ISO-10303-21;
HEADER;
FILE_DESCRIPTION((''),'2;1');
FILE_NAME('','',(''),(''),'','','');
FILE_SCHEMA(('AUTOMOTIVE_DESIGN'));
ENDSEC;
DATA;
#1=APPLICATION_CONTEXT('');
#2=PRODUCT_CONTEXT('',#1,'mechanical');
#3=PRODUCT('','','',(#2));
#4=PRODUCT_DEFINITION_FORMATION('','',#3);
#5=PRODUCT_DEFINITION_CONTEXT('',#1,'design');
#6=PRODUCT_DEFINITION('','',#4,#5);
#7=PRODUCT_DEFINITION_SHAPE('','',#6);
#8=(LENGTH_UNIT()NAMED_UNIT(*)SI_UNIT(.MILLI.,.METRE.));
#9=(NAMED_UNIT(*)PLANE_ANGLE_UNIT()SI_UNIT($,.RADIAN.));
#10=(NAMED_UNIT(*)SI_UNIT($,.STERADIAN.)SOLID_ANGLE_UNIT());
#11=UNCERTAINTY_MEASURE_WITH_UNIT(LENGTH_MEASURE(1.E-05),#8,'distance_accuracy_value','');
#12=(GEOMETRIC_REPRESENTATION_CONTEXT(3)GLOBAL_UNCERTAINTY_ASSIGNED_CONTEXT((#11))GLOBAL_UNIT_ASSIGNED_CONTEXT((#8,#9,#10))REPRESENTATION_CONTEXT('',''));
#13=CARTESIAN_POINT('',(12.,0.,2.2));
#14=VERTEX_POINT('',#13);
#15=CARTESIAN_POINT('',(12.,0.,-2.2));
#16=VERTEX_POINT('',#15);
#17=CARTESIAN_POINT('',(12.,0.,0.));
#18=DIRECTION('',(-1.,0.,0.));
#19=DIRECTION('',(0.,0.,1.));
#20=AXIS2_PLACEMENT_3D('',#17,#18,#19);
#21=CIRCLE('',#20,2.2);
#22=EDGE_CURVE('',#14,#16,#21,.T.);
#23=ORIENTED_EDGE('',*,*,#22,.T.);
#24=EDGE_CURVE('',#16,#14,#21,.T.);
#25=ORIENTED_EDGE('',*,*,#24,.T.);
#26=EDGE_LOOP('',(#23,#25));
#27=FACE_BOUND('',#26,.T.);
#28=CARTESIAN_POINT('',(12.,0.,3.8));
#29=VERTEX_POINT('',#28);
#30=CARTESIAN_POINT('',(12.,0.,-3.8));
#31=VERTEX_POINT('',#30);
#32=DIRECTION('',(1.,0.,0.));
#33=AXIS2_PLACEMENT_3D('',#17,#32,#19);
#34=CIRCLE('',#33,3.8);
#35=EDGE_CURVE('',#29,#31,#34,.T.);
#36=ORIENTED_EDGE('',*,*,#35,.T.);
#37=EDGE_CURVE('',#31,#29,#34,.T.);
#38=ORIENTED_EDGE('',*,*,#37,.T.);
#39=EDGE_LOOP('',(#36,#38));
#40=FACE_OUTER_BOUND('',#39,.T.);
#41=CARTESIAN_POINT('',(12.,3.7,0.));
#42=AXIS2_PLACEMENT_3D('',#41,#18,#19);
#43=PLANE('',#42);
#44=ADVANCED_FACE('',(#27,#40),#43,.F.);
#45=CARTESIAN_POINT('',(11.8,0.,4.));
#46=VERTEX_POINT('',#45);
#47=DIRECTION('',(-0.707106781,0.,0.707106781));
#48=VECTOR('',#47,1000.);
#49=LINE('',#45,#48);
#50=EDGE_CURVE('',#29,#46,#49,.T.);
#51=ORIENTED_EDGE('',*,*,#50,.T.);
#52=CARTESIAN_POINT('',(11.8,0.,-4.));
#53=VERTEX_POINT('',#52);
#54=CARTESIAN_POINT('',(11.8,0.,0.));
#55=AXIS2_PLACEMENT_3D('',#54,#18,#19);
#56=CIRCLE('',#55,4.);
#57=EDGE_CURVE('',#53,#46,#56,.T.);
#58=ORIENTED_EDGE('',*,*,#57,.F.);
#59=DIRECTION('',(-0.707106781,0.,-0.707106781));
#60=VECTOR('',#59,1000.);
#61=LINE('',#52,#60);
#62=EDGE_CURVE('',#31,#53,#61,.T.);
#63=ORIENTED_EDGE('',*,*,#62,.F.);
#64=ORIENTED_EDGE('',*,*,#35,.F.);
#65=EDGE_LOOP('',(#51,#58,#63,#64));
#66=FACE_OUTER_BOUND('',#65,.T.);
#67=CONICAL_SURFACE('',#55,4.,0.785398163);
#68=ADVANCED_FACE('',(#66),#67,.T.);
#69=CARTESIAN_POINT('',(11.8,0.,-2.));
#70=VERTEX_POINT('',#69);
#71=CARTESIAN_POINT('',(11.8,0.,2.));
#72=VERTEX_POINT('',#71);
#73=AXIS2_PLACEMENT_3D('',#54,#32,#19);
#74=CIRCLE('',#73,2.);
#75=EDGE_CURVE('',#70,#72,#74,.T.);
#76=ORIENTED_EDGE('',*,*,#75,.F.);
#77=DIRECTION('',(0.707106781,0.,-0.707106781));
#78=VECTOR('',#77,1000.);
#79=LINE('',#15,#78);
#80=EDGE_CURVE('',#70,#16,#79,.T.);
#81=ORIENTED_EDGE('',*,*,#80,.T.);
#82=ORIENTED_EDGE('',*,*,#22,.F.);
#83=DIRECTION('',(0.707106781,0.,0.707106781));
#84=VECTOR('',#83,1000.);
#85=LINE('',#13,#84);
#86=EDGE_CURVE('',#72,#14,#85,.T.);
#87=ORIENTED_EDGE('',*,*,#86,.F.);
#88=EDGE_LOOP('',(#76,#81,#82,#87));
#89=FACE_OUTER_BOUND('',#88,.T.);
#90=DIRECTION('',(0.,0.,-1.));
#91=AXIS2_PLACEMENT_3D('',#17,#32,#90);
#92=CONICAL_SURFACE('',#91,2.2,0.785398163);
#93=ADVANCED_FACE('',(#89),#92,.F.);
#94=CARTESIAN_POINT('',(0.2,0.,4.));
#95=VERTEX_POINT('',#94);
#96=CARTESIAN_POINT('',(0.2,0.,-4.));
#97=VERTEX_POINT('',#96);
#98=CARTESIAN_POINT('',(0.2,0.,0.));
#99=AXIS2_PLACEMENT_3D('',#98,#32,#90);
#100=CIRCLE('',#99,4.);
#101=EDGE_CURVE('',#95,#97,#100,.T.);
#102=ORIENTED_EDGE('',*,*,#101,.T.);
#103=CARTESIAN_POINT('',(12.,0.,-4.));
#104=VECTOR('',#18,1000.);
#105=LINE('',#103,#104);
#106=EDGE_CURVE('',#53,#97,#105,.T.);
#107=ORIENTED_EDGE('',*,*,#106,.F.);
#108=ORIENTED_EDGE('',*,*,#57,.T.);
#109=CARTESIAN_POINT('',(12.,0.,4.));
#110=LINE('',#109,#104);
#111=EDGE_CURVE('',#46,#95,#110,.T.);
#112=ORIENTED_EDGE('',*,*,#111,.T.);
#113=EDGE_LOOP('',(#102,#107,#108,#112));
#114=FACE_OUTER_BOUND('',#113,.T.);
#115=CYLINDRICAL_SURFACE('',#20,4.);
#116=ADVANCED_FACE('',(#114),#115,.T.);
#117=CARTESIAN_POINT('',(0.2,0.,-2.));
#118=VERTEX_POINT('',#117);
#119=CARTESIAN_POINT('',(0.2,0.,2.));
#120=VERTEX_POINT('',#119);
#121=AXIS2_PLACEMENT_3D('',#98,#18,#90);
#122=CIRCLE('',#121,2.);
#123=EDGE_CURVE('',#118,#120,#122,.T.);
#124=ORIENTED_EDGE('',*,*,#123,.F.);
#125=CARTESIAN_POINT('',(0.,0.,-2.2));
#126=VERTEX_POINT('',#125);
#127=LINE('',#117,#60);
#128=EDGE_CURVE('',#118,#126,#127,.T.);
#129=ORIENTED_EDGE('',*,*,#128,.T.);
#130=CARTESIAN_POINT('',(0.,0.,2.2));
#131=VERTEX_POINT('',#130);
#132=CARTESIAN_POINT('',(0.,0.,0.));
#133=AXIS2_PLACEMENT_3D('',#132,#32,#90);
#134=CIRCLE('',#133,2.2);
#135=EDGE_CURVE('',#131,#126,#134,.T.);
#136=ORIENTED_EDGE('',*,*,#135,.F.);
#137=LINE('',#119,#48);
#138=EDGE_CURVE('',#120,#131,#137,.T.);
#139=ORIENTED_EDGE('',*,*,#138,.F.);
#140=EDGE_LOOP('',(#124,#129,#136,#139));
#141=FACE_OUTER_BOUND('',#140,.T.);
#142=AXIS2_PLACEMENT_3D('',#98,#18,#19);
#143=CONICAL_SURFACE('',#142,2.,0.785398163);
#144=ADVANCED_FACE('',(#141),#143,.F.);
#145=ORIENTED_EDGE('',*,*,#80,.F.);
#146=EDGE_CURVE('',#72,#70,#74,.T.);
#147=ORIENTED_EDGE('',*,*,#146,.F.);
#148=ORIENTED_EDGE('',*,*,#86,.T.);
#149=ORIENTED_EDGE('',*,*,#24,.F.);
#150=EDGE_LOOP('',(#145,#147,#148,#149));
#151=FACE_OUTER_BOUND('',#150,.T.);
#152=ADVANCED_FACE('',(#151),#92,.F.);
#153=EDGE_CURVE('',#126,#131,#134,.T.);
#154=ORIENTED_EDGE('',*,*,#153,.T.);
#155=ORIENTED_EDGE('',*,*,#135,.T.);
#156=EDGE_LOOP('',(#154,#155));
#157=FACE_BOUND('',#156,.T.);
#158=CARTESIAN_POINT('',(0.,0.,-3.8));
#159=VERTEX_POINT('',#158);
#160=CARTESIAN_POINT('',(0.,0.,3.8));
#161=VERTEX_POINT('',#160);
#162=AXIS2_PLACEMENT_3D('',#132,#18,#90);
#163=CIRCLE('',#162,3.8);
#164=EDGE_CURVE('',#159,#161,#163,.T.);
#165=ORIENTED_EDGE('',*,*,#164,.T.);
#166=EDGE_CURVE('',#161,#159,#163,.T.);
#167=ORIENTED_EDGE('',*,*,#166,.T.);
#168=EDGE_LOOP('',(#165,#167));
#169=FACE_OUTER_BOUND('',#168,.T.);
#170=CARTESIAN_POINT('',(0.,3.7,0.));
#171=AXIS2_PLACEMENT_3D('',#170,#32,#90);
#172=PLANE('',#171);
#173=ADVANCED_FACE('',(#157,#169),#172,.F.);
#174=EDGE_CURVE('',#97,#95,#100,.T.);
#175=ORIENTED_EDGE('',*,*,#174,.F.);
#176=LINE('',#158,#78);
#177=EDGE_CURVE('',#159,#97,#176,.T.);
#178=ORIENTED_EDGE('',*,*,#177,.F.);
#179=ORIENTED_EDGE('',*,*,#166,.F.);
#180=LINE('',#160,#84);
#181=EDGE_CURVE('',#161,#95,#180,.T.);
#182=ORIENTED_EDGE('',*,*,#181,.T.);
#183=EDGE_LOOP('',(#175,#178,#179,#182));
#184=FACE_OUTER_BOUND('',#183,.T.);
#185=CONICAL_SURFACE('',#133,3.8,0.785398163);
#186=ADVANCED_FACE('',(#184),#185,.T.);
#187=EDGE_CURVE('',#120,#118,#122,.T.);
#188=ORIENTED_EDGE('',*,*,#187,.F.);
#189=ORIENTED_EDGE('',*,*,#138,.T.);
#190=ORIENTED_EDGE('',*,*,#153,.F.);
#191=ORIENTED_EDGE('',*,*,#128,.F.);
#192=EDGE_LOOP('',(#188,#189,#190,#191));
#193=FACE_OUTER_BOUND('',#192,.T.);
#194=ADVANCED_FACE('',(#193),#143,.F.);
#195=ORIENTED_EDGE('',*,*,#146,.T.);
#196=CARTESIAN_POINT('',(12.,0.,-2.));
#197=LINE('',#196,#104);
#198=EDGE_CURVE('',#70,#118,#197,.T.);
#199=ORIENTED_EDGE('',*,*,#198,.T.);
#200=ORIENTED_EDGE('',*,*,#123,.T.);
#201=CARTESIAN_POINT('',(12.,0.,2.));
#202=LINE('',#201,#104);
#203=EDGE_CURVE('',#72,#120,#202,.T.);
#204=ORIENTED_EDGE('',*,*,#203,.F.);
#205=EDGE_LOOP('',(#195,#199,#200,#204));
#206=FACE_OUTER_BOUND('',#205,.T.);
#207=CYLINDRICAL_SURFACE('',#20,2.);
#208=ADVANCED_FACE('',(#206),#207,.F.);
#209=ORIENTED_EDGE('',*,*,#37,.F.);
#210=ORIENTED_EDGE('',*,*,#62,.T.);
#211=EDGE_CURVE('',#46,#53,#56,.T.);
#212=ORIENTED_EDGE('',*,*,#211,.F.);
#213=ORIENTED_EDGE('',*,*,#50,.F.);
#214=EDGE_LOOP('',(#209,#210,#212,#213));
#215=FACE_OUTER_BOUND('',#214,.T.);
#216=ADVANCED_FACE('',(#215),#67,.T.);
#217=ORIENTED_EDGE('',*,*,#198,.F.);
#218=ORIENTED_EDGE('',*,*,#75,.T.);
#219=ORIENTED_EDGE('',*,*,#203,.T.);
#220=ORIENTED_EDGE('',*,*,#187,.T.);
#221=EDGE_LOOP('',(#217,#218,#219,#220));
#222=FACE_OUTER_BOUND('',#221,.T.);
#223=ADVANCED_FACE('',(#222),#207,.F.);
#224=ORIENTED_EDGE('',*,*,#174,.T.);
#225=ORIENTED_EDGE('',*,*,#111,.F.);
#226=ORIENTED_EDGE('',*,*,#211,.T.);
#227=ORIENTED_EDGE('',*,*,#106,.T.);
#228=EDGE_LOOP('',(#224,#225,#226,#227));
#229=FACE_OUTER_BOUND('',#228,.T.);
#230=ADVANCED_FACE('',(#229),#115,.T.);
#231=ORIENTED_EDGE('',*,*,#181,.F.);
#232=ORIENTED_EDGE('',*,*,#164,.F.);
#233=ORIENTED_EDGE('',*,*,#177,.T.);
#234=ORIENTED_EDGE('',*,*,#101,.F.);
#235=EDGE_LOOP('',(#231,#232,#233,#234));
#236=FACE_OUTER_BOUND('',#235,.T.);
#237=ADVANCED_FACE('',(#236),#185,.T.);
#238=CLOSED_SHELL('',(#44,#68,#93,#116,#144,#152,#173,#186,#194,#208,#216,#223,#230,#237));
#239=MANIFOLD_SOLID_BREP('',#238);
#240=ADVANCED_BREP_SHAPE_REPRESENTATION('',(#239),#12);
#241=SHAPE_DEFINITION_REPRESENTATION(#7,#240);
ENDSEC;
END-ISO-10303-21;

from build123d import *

# Parameters (mm, degrees)
CHAMFER1_SIZE = 0.2


with BuildPart() as part:
    # Sketch1 → Revolve1 (revolve)
    with BuildSketch(Plane.XY, mode=Mode.PRIVATE) as revolve1_sk:
        Polygon((0, 3.7), (0, 2), (12, 2), (12, 3.7), (12, 4), (11.7, 4), (0.3, 4), (0, 4), align=None)
    revolve(revolve1_sk.sketch.rotate(Axis((12, 0, 0), (-1, 0, 0)), 270), axis=Axis((12, 0, 0), (-1, 0, 0)))

    # Chamfer1
    chamfer1_edges = [part.edges().sort_by_distance(p)[0] for p in [
        (0, 0, -4),
        (12, 0, -4),
        (12, 0, -2),
        (0, 0, -2),
    ]]
    chamfer(chamfer1_edges, length=CHAMFER1_SIZE)


solid = part.part
